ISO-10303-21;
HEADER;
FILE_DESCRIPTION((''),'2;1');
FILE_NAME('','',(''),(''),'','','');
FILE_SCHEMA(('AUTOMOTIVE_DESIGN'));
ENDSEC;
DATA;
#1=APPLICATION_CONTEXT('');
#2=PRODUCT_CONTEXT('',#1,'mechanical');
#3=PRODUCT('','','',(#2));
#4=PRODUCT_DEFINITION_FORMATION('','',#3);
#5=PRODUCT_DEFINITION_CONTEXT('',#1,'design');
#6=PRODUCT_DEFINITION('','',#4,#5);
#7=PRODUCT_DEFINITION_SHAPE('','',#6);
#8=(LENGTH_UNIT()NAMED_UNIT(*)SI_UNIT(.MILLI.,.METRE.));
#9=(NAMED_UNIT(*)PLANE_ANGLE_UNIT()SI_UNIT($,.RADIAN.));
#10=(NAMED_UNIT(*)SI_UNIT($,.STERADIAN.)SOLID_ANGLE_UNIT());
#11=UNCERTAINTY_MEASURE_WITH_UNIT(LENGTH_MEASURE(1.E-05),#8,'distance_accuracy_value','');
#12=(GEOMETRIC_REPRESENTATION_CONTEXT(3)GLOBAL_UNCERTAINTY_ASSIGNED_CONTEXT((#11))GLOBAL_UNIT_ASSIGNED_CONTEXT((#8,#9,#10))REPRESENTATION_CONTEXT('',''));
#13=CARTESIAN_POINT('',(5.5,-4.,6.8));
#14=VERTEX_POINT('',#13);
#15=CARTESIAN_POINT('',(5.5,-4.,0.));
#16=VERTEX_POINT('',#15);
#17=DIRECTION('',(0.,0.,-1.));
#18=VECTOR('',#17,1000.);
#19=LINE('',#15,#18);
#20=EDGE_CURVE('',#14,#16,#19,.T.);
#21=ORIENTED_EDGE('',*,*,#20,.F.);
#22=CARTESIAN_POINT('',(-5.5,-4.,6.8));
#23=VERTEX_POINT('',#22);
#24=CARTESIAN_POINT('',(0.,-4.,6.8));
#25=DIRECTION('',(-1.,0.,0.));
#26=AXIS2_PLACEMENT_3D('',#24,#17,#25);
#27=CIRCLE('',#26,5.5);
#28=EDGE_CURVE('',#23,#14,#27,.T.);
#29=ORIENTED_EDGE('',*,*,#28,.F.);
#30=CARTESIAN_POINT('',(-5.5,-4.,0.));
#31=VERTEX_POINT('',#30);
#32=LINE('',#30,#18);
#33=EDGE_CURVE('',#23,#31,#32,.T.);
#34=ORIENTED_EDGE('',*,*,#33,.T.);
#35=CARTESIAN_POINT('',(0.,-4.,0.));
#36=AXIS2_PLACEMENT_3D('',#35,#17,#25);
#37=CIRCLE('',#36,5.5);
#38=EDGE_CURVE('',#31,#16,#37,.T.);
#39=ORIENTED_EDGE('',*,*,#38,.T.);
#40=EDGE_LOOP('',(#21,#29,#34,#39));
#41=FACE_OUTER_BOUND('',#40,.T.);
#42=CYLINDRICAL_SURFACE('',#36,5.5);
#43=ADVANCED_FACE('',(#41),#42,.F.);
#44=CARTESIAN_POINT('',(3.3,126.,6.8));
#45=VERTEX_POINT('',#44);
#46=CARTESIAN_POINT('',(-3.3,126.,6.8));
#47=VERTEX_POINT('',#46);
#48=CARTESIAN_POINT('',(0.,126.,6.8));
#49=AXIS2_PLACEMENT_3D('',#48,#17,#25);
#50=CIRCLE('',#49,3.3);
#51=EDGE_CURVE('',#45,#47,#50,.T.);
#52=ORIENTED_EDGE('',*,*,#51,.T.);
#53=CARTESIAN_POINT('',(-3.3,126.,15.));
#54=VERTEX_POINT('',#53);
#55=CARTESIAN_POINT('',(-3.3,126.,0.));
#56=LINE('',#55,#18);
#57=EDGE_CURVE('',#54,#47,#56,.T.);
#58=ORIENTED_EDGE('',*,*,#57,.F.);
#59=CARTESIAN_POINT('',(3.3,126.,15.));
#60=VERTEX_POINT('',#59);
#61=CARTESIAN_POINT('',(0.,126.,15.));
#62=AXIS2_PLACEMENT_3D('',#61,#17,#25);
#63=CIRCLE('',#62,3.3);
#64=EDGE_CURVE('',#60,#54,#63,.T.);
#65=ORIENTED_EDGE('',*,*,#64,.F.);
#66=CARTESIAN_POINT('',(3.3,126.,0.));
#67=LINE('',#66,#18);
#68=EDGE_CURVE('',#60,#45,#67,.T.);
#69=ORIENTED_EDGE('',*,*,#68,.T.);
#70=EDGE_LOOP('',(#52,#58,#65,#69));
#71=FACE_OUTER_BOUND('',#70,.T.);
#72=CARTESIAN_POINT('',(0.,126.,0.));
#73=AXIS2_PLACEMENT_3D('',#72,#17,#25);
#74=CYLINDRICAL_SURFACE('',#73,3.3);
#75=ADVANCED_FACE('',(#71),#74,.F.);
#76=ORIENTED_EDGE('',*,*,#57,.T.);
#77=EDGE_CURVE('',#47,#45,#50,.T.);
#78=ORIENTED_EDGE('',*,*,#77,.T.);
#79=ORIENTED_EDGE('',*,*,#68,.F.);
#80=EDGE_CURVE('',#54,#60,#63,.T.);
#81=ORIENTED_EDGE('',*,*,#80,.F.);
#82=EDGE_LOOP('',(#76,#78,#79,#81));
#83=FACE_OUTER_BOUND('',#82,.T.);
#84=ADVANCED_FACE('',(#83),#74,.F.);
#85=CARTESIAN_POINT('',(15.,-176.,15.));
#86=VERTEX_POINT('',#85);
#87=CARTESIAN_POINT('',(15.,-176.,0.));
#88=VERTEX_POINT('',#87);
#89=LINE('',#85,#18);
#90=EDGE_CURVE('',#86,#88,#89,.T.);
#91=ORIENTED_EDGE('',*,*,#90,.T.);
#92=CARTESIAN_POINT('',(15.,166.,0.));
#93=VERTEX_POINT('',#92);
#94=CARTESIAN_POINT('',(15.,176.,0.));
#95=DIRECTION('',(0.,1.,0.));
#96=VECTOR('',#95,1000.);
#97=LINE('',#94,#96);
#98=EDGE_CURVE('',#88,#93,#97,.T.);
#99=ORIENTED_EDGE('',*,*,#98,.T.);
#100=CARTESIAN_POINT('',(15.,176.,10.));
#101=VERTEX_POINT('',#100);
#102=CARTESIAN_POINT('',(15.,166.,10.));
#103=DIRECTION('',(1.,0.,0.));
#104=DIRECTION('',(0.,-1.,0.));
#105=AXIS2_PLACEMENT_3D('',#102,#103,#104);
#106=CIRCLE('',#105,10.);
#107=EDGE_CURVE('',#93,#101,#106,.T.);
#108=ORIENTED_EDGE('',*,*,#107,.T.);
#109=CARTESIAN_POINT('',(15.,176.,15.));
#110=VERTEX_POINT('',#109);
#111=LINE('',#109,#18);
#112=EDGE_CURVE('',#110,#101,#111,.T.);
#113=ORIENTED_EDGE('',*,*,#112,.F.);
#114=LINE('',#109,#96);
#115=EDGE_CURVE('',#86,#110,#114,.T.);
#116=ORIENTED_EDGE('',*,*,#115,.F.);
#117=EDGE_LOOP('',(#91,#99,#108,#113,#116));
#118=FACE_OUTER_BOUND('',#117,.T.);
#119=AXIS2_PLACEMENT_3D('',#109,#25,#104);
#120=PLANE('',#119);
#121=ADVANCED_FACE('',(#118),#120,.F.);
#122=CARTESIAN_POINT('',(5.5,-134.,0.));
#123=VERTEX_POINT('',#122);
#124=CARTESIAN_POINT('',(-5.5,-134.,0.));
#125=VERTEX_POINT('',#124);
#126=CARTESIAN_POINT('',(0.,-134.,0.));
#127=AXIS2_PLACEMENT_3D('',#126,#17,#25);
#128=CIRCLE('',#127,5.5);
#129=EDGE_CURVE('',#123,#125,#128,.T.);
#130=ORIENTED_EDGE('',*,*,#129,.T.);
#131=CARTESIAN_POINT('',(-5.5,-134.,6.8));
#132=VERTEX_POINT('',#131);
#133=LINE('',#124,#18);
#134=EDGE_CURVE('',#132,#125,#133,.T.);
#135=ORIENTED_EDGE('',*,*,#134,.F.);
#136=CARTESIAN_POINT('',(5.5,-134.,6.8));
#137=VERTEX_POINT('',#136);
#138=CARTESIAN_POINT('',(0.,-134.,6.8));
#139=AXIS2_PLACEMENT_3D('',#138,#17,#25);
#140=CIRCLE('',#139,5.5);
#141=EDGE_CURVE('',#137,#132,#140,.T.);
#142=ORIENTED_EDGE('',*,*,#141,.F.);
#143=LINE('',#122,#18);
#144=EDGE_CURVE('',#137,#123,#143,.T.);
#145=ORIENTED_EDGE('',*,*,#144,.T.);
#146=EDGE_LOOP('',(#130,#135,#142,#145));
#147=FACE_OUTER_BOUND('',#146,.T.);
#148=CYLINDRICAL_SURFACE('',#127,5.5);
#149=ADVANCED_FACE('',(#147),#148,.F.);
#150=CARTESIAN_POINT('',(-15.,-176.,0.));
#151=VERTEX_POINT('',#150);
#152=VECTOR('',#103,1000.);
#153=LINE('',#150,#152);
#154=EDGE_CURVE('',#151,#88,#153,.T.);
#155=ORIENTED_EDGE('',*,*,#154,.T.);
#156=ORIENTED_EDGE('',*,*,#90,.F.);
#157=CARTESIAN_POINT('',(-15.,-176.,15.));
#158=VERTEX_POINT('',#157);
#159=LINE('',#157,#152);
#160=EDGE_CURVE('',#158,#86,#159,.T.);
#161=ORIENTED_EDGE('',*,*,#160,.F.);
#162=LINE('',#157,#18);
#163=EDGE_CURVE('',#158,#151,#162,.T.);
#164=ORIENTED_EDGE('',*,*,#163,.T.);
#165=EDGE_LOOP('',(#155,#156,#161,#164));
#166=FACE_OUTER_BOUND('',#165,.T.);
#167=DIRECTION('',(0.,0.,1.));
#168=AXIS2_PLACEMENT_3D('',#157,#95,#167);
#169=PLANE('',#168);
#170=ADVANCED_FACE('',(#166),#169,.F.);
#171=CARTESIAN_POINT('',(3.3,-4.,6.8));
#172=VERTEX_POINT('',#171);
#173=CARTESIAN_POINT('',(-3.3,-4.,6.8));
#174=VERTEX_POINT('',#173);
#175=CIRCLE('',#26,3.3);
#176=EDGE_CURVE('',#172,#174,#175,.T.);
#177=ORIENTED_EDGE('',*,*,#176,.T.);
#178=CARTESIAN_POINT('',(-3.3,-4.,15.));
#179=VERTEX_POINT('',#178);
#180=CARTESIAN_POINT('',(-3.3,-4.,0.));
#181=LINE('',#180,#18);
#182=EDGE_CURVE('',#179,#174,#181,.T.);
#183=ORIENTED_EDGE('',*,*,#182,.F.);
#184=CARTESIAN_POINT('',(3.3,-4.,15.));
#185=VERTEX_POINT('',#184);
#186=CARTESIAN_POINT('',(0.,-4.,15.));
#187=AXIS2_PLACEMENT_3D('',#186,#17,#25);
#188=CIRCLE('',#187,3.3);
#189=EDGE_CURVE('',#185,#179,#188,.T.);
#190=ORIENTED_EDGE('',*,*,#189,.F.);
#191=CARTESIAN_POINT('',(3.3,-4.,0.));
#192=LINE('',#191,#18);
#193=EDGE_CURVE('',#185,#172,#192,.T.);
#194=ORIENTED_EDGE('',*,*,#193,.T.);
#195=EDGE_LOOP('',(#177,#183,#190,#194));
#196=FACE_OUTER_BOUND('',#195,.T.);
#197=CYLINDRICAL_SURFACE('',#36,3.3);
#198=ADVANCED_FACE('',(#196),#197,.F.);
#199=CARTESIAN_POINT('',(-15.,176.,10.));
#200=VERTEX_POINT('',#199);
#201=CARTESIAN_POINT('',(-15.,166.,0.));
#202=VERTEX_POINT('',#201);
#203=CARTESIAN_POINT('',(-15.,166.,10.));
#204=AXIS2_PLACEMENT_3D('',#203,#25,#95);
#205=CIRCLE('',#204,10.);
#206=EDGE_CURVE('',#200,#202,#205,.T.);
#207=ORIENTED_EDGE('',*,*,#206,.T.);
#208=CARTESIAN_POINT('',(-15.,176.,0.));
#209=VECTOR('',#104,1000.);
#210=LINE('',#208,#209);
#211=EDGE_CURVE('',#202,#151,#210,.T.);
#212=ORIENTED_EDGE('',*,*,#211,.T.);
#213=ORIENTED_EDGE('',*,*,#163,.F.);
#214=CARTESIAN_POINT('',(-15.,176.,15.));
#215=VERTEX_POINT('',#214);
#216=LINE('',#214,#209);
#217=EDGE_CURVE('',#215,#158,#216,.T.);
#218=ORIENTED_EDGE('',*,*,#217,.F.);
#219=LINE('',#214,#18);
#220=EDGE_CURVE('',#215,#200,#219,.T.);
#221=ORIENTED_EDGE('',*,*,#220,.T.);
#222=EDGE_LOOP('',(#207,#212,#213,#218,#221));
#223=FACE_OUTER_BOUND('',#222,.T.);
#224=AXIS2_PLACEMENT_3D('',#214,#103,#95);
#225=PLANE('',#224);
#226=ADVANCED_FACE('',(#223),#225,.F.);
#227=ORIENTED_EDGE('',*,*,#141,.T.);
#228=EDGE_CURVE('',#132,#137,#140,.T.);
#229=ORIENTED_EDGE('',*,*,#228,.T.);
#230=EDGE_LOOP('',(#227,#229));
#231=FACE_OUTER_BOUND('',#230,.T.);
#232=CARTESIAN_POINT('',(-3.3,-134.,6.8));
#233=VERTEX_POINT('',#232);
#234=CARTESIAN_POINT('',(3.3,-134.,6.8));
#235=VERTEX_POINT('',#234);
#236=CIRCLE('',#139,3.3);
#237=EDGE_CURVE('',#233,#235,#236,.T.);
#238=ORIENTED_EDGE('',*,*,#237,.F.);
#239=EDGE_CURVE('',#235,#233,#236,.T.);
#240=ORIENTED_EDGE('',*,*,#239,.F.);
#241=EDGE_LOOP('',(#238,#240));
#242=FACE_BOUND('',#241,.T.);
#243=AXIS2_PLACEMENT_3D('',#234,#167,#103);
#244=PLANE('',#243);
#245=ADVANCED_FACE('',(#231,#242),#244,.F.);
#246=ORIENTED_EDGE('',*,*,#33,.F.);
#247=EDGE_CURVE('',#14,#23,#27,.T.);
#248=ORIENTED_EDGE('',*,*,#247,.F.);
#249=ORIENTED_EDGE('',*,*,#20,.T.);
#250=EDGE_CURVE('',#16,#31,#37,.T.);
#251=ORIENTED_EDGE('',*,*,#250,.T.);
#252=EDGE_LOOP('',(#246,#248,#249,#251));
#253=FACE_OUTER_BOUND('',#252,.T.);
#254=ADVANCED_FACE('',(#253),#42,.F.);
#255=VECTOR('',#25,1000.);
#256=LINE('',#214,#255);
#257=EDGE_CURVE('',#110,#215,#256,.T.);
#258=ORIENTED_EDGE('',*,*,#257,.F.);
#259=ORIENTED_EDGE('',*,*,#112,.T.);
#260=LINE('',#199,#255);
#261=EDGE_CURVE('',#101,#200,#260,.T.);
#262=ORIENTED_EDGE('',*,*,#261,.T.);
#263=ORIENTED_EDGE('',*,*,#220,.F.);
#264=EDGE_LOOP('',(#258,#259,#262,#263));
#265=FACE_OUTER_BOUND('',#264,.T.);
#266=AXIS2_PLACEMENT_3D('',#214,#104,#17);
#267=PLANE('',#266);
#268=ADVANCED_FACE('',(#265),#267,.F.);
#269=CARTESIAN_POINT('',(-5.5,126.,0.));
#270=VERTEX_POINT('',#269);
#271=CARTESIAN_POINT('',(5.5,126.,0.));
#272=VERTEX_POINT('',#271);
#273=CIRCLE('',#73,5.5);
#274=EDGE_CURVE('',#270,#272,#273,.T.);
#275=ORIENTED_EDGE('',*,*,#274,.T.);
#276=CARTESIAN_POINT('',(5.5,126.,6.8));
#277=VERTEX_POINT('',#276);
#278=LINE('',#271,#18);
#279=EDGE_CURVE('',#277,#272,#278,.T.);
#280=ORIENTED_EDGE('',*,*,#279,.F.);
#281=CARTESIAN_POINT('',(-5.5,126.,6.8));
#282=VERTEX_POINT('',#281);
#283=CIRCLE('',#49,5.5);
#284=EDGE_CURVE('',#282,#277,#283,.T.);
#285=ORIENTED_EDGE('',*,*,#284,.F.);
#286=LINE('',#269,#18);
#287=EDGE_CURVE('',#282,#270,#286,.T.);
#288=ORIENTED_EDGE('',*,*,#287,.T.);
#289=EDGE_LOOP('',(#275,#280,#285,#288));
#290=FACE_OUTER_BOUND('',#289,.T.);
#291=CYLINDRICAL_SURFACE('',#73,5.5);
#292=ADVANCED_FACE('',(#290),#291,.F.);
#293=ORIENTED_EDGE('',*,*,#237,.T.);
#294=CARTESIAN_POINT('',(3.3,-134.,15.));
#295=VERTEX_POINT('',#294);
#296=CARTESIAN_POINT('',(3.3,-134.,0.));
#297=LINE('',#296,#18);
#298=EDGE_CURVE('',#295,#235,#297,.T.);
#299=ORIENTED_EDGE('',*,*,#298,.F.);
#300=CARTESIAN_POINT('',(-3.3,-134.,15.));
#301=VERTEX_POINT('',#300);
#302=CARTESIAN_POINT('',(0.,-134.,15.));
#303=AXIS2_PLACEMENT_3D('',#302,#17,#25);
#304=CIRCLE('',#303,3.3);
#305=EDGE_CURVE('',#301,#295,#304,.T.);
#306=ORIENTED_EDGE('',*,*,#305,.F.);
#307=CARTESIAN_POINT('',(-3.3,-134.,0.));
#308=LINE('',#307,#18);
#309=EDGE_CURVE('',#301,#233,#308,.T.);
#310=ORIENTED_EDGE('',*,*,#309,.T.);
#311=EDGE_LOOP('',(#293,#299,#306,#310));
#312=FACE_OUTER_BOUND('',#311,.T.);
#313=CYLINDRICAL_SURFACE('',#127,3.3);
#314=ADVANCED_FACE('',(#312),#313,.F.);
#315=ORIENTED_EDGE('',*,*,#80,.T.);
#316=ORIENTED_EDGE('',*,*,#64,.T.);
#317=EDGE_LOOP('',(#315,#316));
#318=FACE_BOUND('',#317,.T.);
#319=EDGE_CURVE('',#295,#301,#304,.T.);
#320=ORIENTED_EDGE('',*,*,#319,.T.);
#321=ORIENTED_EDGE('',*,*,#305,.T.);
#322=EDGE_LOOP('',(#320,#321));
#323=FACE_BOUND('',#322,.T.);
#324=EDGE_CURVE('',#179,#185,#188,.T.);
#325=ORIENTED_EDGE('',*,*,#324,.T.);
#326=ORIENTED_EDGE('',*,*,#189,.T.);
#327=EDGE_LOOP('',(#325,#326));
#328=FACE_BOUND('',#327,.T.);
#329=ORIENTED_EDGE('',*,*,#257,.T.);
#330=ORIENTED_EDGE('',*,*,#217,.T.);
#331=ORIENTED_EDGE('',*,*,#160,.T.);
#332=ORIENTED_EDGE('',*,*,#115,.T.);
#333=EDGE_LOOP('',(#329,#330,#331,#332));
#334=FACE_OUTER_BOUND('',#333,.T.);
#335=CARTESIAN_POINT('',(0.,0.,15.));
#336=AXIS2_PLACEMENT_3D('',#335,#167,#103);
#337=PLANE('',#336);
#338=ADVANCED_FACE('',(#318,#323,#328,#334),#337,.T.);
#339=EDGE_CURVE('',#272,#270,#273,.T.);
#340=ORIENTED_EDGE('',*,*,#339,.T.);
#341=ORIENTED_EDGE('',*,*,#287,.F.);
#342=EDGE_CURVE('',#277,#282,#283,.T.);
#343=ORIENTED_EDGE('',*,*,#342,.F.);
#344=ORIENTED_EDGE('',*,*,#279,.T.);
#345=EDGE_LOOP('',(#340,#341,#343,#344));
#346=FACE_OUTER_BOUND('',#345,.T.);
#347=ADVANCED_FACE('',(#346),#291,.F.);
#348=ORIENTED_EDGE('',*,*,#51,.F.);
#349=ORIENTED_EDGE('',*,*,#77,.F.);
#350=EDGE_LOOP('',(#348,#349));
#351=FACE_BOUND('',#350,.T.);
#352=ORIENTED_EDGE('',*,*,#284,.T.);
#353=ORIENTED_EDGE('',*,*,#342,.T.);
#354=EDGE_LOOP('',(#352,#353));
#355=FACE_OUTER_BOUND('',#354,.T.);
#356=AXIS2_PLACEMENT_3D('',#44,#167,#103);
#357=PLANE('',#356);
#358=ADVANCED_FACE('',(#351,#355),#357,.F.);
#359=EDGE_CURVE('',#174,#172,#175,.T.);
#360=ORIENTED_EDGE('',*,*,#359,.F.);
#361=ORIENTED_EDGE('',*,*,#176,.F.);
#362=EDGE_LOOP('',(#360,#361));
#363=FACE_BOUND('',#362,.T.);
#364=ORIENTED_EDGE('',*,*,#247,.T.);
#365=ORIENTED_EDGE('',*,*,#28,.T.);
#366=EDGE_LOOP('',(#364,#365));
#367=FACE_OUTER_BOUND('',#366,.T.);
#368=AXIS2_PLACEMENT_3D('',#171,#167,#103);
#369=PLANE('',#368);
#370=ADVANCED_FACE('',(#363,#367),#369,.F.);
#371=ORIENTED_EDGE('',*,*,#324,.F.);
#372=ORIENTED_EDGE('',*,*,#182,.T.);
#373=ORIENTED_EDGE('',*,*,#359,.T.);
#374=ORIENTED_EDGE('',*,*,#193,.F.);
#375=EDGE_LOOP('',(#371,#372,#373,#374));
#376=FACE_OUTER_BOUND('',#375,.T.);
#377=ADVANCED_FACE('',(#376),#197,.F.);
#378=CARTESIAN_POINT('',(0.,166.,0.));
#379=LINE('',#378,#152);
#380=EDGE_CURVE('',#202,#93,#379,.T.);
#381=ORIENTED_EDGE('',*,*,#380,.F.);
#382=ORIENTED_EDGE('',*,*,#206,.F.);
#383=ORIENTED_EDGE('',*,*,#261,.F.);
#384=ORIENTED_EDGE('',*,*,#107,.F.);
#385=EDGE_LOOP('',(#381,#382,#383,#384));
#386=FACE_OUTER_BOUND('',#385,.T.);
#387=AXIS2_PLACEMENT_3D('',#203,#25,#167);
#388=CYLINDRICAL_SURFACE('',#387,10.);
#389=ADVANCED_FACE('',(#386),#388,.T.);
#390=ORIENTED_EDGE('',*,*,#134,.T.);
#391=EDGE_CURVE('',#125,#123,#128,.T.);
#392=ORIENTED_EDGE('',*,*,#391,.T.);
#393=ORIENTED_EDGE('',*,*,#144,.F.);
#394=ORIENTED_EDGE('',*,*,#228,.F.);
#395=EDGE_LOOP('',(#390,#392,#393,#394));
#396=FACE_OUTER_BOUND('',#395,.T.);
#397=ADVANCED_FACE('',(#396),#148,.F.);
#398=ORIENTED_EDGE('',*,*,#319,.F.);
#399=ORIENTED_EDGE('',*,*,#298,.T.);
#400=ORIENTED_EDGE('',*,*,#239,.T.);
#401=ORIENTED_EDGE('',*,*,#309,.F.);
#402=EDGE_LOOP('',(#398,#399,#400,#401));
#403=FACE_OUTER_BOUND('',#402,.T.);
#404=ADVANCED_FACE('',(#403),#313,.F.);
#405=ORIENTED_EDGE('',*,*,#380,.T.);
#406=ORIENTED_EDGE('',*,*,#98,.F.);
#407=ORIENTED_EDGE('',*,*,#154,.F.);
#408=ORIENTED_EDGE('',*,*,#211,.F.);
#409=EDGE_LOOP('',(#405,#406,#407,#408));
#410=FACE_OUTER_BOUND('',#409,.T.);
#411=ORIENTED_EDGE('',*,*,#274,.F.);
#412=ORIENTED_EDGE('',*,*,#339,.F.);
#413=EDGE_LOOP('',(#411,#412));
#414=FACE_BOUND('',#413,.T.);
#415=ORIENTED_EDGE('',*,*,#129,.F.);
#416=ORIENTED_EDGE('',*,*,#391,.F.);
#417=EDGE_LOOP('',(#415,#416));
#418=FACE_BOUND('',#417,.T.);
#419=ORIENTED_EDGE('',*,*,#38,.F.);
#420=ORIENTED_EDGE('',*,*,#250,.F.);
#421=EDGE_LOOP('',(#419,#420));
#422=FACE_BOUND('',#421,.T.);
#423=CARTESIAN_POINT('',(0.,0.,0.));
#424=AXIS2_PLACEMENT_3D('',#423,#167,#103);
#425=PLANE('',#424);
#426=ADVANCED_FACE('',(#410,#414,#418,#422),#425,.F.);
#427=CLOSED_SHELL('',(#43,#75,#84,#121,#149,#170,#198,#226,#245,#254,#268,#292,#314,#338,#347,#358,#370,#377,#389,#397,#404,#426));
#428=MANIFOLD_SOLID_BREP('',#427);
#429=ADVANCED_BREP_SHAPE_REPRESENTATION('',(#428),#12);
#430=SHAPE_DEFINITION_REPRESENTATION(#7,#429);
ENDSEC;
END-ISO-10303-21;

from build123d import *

# Parameters (mm, degrees)
SKETCH_1_W                = 30
SKETCH_1_H                = 352
EXTRUDE_1_DEPTH           = 15
HOLE_WIZARD_1_D           = 6.6
HOLE_WIZARD_1_CBORE_D     = 11
HOLE_WIZARD_1_CBORE_DEPTH = 6.8
FILLET_1_R                = 10


with BuildPart() as part:
    # 草图1 → 凸台-拉伸1 (new body)
    with BuildSketch(Plane.XY):
        Rectangle(SKETCH_1_W, SKETCH_1_H)
    extrude(amount=EXTRUDE_1_DEPTH)

    # 打孔尺寸(%根据)内六角圆柱头螺钉的类型1 (through all)
    with Locations(Plane(origin=(0, 0, 0), x_dir=(-1, 0, 0), z_dir=(0, 0, -1))):
        with Locations((0, 126), (0, -4), (0, -134)):
            CounterBoreHole(HOLE_WIZARD_1_D / 2, HOLE_WIZARD_1_CBORE_D / 2, HOLE_WIZARD_1_CBORE_DEPTH)

    # 圆角1
    fillet_1_edges = [part.edges().sort_by_distance(p)[0] for p in [
        (0, 176, 0),
    ]]
    fillet(fillet_1_edges, radius=FILLET_1_R)


solid = part.part
